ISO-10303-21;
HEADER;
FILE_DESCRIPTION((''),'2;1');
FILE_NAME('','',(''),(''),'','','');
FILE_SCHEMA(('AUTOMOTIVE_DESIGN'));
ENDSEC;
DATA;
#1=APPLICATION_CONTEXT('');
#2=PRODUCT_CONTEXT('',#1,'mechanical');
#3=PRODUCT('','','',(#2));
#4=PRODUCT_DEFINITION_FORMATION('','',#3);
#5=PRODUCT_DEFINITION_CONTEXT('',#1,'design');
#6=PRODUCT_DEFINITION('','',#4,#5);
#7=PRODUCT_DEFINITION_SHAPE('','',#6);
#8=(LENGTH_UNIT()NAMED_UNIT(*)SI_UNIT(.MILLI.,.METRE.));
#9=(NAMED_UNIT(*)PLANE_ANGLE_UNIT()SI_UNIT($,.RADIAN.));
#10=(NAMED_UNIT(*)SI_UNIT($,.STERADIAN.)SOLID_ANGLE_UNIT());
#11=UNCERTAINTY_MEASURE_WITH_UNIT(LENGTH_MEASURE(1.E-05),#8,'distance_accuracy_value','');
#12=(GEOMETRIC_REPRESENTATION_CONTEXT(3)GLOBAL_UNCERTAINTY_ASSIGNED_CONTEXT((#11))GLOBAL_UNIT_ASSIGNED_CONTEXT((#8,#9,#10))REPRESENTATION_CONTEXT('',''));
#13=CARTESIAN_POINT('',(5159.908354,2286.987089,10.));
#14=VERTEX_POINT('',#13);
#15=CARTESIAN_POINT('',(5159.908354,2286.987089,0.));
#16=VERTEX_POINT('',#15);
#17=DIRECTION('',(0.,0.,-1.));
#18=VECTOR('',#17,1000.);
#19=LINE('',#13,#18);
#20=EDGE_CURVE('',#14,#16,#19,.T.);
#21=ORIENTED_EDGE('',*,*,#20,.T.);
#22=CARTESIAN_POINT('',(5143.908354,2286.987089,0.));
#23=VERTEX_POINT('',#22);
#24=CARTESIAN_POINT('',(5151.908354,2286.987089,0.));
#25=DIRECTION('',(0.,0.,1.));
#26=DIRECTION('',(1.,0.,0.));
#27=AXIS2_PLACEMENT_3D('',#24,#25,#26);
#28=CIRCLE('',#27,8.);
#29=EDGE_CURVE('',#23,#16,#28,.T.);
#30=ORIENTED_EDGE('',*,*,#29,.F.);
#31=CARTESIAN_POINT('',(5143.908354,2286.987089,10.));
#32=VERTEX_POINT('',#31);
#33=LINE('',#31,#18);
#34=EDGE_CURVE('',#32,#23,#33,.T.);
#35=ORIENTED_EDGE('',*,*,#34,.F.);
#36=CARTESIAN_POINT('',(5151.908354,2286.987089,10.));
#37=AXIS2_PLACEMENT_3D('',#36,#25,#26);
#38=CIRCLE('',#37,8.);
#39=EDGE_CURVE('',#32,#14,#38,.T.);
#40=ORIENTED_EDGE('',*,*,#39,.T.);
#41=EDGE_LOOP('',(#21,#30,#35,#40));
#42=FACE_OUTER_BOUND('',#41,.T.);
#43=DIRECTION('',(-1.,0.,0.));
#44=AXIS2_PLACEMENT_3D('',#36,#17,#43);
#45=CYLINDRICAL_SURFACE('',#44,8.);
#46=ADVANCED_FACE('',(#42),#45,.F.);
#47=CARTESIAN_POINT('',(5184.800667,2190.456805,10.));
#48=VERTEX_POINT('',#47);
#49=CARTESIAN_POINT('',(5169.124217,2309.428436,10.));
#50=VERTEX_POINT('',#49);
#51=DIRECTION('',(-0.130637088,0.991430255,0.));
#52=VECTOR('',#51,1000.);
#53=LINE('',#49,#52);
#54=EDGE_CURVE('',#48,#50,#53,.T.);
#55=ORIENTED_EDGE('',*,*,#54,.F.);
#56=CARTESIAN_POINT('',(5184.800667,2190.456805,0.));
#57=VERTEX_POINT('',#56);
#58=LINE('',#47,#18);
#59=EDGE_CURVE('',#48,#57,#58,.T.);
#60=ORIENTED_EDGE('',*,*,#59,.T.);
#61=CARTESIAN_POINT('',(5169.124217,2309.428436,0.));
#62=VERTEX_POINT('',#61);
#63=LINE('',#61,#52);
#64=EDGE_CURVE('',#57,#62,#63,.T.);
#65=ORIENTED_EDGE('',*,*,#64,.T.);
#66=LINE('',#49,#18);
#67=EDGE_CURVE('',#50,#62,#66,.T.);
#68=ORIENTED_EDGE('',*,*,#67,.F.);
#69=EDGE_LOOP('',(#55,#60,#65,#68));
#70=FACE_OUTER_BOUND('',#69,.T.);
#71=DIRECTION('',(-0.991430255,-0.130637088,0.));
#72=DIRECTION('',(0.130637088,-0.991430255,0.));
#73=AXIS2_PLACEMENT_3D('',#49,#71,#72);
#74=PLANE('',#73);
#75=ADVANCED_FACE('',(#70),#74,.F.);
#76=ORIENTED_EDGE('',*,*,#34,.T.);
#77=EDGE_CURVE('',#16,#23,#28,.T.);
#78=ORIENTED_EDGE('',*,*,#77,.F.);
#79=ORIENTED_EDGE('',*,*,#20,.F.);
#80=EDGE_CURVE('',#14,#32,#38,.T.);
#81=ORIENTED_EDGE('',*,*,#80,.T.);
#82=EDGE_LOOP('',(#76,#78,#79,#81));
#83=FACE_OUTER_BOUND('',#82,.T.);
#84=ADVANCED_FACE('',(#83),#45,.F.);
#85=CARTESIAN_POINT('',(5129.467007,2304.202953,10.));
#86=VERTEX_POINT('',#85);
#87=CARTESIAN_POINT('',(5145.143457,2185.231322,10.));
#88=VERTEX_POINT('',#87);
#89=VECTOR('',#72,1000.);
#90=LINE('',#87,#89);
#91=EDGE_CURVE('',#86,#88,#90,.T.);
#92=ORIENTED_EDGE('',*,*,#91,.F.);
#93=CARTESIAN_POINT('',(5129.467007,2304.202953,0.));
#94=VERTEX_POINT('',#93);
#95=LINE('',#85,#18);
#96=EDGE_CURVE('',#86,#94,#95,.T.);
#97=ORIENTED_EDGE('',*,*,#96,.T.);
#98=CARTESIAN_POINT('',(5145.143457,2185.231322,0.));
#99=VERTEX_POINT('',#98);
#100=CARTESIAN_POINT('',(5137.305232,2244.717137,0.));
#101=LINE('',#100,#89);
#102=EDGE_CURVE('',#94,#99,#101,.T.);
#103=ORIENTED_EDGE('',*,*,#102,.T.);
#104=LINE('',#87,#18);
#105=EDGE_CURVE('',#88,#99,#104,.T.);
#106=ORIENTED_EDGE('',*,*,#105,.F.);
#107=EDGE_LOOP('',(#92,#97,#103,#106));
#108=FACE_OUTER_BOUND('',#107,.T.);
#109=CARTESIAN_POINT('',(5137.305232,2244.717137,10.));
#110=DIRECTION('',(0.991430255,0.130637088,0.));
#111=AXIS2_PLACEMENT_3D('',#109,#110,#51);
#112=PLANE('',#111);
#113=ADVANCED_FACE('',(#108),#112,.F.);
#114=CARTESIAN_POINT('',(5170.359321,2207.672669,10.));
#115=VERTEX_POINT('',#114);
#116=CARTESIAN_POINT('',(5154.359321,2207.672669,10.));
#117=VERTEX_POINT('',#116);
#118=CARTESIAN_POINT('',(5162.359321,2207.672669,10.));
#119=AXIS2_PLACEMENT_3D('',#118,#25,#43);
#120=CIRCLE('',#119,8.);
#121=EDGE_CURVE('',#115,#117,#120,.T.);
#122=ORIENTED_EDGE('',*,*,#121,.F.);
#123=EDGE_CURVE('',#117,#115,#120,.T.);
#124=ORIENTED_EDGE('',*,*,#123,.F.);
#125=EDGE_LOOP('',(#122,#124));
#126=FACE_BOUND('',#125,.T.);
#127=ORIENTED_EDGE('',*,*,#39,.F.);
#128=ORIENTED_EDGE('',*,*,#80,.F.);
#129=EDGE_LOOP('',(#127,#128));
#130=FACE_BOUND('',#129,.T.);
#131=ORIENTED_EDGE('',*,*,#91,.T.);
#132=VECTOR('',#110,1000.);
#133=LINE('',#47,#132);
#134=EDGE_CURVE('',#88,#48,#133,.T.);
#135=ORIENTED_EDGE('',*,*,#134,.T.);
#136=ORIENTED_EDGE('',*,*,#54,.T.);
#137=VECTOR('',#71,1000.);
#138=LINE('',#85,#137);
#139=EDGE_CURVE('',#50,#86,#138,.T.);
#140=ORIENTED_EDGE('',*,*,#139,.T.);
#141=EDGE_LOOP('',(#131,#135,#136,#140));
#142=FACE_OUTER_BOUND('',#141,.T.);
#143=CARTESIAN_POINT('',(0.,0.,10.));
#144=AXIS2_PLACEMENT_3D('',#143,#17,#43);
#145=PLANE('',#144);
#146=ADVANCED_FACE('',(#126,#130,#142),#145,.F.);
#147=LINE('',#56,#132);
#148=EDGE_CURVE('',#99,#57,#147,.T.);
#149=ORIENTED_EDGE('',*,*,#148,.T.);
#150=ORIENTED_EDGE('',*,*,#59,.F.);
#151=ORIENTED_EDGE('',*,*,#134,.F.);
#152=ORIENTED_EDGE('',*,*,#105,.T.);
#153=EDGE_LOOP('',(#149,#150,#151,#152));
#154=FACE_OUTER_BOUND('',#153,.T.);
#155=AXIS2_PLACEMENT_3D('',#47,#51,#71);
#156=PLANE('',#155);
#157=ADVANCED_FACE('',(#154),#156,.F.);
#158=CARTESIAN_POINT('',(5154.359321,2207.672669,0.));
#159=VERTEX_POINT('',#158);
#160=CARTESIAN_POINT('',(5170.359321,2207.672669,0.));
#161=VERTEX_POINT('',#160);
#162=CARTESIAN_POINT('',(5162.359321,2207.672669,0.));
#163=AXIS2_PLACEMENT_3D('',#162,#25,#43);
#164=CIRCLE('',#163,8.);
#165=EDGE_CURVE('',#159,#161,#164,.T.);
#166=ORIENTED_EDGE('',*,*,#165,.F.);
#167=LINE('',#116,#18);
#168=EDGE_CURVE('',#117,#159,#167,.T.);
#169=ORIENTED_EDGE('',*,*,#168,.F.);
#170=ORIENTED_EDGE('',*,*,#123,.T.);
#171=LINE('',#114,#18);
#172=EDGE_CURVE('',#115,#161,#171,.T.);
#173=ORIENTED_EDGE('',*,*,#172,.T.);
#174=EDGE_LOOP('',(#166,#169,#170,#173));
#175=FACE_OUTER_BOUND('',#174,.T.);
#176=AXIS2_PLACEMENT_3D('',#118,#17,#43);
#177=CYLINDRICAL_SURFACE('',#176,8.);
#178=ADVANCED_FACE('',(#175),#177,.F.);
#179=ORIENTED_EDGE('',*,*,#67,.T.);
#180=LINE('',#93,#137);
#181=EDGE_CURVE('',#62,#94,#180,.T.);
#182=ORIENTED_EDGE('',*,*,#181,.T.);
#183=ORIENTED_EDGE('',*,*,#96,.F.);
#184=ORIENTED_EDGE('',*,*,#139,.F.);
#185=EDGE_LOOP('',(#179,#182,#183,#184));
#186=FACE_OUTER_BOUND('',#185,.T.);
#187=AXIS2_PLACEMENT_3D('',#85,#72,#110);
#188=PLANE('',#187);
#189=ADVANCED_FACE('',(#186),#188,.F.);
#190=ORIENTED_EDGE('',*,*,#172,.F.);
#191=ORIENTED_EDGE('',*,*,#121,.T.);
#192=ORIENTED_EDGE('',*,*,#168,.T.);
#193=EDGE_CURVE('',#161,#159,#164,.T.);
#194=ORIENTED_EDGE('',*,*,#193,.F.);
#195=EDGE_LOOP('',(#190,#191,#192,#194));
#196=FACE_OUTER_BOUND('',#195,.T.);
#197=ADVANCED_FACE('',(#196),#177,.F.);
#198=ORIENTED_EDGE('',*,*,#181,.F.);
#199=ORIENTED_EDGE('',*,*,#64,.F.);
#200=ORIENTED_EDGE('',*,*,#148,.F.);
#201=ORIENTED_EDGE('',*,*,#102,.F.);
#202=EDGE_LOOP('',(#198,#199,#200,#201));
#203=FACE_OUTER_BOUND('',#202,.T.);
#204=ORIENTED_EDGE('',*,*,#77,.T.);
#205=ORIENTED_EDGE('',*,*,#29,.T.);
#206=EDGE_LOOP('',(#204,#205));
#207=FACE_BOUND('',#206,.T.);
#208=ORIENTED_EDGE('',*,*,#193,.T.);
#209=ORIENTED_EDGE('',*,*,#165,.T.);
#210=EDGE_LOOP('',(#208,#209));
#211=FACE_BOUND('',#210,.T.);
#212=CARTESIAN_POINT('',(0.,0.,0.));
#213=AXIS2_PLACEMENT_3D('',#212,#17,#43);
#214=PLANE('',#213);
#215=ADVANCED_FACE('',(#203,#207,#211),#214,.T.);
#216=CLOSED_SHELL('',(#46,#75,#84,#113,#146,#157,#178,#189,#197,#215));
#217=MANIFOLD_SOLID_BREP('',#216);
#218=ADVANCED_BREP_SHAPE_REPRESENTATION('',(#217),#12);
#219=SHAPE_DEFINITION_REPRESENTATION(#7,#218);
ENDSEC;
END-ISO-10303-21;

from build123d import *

# Parameters (mm, degrees)
SKETCH1_R           = 8
BOSS_EXTRUDE1_DEPTH = 10


with BuildPart() as part:
    # Sketch1 → Boss-Extrude1 (new body)
    with BuildSketch(Plane.XY):
        Polygon((5137.305231976, 2244.717137192), (5129.46700669, 2304.202952513), (5169.124216904, 2309.428436037), (5184.800667476, 2190.456805396), (5145.143457262, 2185.231321872), align=None)
        with Locations((5151.908353559, 2286.987089168)):
            Circle(SKETCH1_R, mode=Mode.SUBTRACT)
        with Locations(Location((5162.359320607, 2207.67266874, 0), (0, 0, 180))):
            Circle(SKETCH1_R, mode=Mode.SUBTRACT)
    extrude(amount=BOSS_EXTRUDE1_DEPTH)


solid = part.part
